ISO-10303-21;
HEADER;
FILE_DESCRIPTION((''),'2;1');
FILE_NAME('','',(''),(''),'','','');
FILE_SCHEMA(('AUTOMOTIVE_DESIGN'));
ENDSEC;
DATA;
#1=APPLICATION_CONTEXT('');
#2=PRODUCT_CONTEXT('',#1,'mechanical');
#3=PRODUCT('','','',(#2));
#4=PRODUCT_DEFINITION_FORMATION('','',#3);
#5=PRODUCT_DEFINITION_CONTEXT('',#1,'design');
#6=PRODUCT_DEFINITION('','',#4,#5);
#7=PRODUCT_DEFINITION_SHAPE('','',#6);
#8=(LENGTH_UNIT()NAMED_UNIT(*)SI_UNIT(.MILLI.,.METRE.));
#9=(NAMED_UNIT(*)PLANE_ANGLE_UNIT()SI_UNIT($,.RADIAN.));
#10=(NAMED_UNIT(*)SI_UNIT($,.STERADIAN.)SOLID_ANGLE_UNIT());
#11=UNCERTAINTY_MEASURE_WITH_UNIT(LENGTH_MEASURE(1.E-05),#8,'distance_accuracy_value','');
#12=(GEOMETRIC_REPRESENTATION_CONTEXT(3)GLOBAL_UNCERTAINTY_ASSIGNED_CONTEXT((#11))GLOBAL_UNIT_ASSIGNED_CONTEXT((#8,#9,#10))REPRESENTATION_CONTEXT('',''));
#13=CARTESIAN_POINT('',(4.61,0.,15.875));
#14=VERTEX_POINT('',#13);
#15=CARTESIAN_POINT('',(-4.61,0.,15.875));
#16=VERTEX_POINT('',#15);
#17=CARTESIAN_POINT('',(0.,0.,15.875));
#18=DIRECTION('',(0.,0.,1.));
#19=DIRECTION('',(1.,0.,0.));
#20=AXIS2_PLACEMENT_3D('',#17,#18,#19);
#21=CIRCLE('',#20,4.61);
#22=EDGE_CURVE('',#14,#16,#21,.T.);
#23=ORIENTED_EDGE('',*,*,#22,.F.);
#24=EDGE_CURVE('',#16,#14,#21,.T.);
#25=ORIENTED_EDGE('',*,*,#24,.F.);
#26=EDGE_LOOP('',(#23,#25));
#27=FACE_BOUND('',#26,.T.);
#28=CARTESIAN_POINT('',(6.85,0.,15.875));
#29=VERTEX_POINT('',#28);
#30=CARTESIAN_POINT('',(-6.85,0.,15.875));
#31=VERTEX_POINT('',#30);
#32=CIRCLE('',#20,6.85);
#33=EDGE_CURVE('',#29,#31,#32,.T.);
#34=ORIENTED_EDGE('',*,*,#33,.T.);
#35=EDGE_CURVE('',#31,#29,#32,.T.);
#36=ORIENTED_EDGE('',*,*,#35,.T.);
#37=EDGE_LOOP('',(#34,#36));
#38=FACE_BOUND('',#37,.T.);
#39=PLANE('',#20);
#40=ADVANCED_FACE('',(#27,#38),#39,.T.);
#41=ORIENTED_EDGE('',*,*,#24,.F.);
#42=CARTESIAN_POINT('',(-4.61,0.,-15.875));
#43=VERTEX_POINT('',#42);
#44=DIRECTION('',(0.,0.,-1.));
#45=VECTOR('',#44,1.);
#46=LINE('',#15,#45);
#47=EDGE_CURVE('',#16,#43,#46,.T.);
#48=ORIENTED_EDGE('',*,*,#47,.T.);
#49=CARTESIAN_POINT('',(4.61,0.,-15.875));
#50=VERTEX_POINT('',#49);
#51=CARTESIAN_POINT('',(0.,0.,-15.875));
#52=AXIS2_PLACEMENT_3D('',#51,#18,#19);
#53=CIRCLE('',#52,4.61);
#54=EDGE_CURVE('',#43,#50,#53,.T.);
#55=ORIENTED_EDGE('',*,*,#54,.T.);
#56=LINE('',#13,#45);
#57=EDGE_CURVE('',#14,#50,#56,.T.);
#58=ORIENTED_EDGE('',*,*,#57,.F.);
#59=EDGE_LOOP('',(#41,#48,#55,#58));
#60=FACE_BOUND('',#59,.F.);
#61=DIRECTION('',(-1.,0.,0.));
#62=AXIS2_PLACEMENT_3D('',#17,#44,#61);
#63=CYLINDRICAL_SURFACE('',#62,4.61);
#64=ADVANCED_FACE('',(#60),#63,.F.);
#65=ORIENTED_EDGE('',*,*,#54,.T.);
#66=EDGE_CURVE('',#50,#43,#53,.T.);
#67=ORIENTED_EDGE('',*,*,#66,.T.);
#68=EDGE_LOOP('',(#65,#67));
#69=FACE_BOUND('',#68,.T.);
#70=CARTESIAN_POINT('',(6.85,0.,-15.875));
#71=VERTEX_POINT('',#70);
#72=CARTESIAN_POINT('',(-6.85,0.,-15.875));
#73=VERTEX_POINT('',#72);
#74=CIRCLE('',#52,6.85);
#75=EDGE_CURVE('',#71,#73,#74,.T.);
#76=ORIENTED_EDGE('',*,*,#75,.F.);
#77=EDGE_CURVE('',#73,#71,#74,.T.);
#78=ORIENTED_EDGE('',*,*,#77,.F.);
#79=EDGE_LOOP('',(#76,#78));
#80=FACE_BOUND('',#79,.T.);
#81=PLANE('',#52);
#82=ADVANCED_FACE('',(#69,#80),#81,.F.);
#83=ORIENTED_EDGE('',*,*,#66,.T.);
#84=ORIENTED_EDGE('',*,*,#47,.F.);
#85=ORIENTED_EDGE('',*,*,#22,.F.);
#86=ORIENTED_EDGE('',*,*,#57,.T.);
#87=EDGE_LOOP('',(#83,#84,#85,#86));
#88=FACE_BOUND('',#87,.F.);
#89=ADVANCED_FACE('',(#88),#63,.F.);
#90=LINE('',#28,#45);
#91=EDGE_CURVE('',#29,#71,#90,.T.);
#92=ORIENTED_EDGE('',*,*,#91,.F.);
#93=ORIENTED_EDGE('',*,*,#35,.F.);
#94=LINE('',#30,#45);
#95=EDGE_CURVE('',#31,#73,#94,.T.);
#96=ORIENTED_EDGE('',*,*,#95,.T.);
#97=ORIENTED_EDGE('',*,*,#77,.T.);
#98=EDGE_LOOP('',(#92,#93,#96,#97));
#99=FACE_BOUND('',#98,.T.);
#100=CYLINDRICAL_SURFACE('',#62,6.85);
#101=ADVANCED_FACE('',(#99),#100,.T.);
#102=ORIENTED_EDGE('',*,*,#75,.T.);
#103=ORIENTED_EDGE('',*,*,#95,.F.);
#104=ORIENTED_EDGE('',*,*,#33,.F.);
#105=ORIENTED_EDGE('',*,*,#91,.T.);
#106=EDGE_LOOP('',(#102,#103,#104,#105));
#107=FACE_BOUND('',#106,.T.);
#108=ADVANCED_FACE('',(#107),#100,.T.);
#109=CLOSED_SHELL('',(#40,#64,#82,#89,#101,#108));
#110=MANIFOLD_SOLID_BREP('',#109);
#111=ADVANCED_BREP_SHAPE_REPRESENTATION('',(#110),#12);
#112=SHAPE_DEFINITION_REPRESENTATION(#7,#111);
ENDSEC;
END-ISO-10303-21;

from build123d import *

# Parameters (mm, degrees)
SKETCH1_R           = 6.85
SKETCH1_R_2         = 4.61
BOSS_EXTRUDE1_DEPTH = 15.875


with BuildPart() as part:
    # Sketch1 → Boss-Extrude1 (new, symmetric)
    with BuildSketch(Plane.XY):
        Circle(SKETCH1_R)
        Circle(SKETCH1_R_2, mode=Mode.SUBTRACT)
    extrude(amount=BOSS_EXTRUDE1_DEPTH, both=True)


solid = part.part
